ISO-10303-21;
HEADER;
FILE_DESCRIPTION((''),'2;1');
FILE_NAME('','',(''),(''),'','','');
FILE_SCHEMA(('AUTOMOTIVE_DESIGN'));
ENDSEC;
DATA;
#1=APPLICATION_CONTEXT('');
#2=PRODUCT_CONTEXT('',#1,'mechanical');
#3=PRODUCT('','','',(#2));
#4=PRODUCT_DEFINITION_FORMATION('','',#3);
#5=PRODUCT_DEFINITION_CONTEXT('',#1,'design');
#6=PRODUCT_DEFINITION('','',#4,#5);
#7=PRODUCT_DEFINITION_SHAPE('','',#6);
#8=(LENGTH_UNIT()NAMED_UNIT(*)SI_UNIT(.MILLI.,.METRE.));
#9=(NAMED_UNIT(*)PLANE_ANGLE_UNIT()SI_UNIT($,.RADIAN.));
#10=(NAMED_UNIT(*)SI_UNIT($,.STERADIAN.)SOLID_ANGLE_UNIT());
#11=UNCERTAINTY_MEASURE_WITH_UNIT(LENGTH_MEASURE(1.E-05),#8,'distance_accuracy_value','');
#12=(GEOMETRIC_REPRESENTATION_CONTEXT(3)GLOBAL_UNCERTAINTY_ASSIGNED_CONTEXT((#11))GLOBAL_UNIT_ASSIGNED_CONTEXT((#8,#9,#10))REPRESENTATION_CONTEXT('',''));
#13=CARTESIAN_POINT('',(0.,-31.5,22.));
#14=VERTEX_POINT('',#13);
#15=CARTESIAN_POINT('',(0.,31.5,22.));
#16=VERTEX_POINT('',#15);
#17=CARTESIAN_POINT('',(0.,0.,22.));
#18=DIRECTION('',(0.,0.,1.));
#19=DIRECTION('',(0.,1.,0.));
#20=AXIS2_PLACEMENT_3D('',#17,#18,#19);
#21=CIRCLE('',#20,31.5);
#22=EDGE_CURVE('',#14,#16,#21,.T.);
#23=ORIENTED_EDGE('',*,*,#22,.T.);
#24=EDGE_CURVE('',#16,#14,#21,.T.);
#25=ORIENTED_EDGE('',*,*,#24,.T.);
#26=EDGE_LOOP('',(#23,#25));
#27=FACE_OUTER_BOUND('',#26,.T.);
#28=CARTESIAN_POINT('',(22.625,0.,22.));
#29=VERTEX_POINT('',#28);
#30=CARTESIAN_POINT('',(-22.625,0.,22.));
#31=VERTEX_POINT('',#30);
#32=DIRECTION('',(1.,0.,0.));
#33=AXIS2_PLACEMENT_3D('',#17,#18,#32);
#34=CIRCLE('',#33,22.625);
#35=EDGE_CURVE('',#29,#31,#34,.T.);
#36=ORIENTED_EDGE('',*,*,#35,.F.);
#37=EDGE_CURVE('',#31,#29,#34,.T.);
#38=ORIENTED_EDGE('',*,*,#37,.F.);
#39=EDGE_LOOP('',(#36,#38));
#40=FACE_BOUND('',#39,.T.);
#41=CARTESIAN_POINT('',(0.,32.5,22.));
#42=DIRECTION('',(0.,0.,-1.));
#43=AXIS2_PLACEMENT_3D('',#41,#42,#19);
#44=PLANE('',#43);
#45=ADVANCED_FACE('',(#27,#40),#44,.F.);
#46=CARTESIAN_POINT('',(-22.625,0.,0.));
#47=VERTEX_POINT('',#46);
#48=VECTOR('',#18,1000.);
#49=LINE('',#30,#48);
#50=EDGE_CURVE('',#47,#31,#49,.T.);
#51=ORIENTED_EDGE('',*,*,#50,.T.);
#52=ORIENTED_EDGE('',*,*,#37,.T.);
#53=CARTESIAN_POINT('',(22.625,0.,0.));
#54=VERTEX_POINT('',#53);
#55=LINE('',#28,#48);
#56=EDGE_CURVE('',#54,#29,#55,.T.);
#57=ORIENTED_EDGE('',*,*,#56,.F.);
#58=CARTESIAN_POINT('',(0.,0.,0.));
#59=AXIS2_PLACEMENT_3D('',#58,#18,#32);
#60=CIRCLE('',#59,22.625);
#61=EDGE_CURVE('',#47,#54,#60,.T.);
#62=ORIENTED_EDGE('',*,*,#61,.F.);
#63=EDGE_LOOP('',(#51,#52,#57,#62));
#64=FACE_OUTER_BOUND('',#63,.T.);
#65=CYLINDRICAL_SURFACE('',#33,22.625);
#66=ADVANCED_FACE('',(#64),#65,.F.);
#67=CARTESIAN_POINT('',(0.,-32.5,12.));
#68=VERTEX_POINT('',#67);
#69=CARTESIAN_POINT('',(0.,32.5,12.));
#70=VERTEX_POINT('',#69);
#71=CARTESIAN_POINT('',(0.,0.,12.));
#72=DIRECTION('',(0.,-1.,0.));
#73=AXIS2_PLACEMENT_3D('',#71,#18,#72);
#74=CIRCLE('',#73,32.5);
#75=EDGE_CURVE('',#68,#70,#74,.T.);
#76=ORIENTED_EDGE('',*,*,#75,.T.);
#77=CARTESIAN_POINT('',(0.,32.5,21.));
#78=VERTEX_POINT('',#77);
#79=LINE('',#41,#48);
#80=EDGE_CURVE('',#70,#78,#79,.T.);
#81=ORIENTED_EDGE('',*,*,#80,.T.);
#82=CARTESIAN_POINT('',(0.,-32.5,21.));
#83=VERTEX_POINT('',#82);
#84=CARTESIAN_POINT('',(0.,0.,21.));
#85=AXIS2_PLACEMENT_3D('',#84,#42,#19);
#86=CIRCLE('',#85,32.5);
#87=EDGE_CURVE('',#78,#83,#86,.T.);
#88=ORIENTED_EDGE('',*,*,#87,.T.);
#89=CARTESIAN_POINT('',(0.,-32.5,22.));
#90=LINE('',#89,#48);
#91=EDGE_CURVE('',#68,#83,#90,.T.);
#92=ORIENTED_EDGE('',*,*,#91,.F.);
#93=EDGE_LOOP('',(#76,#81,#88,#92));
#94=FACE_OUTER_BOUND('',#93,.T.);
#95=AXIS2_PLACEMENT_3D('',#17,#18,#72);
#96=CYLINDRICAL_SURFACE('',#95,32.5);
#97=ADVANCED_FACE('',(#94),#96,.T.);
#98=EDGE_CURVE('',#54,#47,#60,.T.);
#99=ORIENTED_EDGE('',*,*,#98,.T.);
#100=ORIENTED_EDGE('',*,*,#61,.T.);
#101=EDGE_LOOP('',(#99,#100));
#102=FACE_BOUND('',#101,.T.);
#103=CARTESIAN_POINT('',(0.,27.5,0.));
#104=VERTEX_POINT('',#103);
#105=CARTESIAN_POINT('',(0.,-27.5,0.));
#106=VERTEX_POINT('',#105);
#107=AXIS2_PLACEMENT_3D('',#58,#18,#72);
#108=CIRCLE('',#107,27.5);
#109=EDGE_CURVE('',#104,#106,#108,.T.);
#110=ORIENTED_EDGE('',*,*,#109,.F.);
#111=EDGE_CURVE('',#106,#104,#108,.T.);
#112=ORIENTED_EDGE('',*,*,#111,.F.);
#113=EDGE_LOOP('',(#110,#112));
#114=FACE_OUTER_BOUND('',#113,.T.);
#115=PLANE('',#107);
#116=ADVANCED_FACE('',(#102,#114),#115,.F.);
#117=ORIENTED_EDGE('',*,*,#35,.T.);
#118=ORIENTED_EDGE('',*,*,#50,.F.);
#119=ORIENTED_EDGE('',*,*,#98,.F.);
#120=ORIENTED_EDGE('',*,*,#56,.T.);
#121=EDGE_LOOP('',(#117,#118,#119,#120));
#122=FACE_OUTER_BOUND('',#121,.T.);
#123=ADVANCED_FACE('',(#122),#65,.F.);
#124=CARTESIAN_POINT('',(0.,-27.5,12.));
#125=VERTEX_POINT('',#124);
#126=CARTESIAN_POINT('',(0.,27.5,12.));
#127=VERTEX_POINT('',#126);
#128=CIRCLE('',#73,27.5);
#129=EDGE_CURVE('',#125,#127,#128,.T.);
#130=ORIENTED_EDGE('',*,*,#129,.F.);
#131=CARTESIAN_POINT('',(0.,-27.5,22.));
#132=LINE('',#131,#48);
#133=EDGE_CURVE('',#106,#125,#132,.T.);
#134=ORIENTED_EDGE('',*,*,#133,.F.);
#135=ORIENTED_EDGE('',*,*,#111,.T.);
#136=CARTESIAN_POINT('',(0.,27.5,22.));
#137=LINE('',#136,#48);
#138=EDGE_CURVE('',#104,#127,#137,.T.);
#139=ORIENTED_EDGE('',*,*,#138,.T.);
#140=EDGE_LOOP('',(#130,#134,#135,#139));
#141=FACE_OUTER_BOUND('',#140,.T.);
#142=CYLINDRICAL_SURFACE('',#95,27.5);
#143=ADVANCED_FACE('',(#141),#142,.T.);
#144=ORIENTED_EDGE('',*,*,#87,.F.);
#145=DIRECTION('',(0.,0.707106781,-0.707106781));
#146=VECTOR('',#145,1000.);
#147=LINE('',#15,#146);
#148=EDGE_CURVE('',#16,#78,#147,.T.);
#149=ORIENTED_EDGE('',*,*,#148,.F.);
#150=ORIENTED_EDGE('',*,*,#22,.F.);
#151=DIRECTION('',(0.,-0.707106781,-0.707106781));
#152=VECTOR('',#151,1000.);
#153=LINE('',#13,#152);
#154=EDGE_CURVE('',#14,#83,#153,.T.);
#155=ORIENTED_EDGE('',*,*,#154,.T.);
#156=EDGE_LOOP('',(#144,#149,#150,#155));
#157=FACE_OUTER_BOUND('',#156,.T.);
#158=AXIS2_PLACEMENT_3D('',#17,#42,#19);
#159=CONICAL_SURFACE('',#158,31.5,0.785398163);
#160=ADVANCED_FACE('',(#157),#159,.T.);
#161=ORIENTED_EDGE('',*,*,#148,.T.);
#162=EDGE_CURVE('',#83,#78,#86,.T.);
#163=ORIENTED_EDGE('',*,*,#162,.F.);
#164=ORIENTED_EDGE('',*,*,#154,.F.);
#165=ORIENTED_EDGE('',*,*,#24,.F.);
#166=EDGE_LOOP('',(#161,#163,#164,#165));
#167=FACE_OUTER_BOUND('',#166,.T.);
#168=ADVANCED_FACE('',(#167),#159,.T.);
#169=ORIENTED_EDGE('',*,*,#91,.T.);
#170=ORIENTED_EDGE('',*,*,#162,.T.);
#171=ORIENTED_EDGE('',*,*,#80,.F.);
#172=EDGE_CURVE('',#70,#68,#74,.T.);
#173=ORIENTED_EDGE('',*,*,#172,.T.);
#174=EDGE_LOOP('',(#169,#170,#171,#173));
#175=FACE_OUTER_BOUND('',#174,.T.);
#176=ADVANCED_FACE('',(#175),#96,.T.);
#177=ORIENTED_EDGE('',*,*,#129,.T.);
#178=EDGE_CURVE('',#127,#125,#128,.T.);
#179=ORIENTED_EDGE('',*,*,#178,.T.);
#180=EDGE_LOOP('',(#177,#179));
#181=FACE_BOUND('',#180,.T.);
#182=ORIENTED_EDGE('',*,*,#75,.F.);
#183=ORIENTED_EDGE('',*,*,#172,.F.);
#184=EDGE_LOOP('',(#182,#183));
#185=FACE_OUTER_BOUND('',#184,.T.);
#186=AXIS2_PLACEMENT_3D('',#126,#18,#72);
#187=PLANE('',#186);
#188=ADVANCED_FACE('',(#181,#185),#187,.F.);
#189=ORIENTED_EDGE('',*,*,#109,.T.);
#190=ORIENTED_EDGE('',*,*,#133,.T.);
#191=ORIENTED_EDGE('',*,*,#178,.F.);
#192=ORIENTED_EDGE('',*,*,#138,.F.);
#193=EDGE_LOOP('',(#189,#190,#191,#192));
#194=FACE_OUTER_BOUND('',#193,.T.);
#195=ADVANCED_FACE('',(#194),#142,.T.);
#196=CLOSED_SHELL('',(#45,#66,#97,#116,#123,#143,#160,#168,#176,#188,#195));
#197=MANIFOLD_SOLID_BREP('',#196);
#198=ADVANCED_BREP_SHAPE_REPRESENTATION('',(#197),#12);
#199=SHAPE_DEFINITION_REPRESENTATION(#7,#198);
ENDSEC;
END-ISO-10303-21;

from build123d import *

# Parameters (mm, degrees)
G1_1_2_TAPPED_HOLE1_D = 45.25
CHAMFER1_SIZE         = 1


with BuildPart() as part:
    # Sketch1 → Revolve1 (revolve)
    with BuildSketch(Plane(origin=(0, 0, 0), x_dir=(0, 0, -1), z_dir=(1, 0, 0)), mode=Mode.PRIVATE) as revolve1_sk:
        Polygon((0, 0), (0, 27.5), (-12, 27.5), (-12, 32.5), (-22, 32.5), (-22, 0), align=None)
    revolve(revolve1_sk.sketch.rotate(Axis((0, 0, 22), (0, 0, -1)), 180), axis=Axis((0, 0, 22), (0, 0, -1)))

    # G1-1/2 Tapped Hole1 (through all)
    with Locations(Plane.XY.offset(22)):
        with Locations((0, 0)):
            Hole(G1_1_2_TAPPED_HOLE1_D / 2)

    # Chamfer1
    chamfer1_edges = [part.edges().sort_by_distance(p)[0] for p in [
        (0, 32.5, 22),
    ]]
    chamfer(chamfer1_edges, length=CHAMFER1_SIZE)


solid = part.part
